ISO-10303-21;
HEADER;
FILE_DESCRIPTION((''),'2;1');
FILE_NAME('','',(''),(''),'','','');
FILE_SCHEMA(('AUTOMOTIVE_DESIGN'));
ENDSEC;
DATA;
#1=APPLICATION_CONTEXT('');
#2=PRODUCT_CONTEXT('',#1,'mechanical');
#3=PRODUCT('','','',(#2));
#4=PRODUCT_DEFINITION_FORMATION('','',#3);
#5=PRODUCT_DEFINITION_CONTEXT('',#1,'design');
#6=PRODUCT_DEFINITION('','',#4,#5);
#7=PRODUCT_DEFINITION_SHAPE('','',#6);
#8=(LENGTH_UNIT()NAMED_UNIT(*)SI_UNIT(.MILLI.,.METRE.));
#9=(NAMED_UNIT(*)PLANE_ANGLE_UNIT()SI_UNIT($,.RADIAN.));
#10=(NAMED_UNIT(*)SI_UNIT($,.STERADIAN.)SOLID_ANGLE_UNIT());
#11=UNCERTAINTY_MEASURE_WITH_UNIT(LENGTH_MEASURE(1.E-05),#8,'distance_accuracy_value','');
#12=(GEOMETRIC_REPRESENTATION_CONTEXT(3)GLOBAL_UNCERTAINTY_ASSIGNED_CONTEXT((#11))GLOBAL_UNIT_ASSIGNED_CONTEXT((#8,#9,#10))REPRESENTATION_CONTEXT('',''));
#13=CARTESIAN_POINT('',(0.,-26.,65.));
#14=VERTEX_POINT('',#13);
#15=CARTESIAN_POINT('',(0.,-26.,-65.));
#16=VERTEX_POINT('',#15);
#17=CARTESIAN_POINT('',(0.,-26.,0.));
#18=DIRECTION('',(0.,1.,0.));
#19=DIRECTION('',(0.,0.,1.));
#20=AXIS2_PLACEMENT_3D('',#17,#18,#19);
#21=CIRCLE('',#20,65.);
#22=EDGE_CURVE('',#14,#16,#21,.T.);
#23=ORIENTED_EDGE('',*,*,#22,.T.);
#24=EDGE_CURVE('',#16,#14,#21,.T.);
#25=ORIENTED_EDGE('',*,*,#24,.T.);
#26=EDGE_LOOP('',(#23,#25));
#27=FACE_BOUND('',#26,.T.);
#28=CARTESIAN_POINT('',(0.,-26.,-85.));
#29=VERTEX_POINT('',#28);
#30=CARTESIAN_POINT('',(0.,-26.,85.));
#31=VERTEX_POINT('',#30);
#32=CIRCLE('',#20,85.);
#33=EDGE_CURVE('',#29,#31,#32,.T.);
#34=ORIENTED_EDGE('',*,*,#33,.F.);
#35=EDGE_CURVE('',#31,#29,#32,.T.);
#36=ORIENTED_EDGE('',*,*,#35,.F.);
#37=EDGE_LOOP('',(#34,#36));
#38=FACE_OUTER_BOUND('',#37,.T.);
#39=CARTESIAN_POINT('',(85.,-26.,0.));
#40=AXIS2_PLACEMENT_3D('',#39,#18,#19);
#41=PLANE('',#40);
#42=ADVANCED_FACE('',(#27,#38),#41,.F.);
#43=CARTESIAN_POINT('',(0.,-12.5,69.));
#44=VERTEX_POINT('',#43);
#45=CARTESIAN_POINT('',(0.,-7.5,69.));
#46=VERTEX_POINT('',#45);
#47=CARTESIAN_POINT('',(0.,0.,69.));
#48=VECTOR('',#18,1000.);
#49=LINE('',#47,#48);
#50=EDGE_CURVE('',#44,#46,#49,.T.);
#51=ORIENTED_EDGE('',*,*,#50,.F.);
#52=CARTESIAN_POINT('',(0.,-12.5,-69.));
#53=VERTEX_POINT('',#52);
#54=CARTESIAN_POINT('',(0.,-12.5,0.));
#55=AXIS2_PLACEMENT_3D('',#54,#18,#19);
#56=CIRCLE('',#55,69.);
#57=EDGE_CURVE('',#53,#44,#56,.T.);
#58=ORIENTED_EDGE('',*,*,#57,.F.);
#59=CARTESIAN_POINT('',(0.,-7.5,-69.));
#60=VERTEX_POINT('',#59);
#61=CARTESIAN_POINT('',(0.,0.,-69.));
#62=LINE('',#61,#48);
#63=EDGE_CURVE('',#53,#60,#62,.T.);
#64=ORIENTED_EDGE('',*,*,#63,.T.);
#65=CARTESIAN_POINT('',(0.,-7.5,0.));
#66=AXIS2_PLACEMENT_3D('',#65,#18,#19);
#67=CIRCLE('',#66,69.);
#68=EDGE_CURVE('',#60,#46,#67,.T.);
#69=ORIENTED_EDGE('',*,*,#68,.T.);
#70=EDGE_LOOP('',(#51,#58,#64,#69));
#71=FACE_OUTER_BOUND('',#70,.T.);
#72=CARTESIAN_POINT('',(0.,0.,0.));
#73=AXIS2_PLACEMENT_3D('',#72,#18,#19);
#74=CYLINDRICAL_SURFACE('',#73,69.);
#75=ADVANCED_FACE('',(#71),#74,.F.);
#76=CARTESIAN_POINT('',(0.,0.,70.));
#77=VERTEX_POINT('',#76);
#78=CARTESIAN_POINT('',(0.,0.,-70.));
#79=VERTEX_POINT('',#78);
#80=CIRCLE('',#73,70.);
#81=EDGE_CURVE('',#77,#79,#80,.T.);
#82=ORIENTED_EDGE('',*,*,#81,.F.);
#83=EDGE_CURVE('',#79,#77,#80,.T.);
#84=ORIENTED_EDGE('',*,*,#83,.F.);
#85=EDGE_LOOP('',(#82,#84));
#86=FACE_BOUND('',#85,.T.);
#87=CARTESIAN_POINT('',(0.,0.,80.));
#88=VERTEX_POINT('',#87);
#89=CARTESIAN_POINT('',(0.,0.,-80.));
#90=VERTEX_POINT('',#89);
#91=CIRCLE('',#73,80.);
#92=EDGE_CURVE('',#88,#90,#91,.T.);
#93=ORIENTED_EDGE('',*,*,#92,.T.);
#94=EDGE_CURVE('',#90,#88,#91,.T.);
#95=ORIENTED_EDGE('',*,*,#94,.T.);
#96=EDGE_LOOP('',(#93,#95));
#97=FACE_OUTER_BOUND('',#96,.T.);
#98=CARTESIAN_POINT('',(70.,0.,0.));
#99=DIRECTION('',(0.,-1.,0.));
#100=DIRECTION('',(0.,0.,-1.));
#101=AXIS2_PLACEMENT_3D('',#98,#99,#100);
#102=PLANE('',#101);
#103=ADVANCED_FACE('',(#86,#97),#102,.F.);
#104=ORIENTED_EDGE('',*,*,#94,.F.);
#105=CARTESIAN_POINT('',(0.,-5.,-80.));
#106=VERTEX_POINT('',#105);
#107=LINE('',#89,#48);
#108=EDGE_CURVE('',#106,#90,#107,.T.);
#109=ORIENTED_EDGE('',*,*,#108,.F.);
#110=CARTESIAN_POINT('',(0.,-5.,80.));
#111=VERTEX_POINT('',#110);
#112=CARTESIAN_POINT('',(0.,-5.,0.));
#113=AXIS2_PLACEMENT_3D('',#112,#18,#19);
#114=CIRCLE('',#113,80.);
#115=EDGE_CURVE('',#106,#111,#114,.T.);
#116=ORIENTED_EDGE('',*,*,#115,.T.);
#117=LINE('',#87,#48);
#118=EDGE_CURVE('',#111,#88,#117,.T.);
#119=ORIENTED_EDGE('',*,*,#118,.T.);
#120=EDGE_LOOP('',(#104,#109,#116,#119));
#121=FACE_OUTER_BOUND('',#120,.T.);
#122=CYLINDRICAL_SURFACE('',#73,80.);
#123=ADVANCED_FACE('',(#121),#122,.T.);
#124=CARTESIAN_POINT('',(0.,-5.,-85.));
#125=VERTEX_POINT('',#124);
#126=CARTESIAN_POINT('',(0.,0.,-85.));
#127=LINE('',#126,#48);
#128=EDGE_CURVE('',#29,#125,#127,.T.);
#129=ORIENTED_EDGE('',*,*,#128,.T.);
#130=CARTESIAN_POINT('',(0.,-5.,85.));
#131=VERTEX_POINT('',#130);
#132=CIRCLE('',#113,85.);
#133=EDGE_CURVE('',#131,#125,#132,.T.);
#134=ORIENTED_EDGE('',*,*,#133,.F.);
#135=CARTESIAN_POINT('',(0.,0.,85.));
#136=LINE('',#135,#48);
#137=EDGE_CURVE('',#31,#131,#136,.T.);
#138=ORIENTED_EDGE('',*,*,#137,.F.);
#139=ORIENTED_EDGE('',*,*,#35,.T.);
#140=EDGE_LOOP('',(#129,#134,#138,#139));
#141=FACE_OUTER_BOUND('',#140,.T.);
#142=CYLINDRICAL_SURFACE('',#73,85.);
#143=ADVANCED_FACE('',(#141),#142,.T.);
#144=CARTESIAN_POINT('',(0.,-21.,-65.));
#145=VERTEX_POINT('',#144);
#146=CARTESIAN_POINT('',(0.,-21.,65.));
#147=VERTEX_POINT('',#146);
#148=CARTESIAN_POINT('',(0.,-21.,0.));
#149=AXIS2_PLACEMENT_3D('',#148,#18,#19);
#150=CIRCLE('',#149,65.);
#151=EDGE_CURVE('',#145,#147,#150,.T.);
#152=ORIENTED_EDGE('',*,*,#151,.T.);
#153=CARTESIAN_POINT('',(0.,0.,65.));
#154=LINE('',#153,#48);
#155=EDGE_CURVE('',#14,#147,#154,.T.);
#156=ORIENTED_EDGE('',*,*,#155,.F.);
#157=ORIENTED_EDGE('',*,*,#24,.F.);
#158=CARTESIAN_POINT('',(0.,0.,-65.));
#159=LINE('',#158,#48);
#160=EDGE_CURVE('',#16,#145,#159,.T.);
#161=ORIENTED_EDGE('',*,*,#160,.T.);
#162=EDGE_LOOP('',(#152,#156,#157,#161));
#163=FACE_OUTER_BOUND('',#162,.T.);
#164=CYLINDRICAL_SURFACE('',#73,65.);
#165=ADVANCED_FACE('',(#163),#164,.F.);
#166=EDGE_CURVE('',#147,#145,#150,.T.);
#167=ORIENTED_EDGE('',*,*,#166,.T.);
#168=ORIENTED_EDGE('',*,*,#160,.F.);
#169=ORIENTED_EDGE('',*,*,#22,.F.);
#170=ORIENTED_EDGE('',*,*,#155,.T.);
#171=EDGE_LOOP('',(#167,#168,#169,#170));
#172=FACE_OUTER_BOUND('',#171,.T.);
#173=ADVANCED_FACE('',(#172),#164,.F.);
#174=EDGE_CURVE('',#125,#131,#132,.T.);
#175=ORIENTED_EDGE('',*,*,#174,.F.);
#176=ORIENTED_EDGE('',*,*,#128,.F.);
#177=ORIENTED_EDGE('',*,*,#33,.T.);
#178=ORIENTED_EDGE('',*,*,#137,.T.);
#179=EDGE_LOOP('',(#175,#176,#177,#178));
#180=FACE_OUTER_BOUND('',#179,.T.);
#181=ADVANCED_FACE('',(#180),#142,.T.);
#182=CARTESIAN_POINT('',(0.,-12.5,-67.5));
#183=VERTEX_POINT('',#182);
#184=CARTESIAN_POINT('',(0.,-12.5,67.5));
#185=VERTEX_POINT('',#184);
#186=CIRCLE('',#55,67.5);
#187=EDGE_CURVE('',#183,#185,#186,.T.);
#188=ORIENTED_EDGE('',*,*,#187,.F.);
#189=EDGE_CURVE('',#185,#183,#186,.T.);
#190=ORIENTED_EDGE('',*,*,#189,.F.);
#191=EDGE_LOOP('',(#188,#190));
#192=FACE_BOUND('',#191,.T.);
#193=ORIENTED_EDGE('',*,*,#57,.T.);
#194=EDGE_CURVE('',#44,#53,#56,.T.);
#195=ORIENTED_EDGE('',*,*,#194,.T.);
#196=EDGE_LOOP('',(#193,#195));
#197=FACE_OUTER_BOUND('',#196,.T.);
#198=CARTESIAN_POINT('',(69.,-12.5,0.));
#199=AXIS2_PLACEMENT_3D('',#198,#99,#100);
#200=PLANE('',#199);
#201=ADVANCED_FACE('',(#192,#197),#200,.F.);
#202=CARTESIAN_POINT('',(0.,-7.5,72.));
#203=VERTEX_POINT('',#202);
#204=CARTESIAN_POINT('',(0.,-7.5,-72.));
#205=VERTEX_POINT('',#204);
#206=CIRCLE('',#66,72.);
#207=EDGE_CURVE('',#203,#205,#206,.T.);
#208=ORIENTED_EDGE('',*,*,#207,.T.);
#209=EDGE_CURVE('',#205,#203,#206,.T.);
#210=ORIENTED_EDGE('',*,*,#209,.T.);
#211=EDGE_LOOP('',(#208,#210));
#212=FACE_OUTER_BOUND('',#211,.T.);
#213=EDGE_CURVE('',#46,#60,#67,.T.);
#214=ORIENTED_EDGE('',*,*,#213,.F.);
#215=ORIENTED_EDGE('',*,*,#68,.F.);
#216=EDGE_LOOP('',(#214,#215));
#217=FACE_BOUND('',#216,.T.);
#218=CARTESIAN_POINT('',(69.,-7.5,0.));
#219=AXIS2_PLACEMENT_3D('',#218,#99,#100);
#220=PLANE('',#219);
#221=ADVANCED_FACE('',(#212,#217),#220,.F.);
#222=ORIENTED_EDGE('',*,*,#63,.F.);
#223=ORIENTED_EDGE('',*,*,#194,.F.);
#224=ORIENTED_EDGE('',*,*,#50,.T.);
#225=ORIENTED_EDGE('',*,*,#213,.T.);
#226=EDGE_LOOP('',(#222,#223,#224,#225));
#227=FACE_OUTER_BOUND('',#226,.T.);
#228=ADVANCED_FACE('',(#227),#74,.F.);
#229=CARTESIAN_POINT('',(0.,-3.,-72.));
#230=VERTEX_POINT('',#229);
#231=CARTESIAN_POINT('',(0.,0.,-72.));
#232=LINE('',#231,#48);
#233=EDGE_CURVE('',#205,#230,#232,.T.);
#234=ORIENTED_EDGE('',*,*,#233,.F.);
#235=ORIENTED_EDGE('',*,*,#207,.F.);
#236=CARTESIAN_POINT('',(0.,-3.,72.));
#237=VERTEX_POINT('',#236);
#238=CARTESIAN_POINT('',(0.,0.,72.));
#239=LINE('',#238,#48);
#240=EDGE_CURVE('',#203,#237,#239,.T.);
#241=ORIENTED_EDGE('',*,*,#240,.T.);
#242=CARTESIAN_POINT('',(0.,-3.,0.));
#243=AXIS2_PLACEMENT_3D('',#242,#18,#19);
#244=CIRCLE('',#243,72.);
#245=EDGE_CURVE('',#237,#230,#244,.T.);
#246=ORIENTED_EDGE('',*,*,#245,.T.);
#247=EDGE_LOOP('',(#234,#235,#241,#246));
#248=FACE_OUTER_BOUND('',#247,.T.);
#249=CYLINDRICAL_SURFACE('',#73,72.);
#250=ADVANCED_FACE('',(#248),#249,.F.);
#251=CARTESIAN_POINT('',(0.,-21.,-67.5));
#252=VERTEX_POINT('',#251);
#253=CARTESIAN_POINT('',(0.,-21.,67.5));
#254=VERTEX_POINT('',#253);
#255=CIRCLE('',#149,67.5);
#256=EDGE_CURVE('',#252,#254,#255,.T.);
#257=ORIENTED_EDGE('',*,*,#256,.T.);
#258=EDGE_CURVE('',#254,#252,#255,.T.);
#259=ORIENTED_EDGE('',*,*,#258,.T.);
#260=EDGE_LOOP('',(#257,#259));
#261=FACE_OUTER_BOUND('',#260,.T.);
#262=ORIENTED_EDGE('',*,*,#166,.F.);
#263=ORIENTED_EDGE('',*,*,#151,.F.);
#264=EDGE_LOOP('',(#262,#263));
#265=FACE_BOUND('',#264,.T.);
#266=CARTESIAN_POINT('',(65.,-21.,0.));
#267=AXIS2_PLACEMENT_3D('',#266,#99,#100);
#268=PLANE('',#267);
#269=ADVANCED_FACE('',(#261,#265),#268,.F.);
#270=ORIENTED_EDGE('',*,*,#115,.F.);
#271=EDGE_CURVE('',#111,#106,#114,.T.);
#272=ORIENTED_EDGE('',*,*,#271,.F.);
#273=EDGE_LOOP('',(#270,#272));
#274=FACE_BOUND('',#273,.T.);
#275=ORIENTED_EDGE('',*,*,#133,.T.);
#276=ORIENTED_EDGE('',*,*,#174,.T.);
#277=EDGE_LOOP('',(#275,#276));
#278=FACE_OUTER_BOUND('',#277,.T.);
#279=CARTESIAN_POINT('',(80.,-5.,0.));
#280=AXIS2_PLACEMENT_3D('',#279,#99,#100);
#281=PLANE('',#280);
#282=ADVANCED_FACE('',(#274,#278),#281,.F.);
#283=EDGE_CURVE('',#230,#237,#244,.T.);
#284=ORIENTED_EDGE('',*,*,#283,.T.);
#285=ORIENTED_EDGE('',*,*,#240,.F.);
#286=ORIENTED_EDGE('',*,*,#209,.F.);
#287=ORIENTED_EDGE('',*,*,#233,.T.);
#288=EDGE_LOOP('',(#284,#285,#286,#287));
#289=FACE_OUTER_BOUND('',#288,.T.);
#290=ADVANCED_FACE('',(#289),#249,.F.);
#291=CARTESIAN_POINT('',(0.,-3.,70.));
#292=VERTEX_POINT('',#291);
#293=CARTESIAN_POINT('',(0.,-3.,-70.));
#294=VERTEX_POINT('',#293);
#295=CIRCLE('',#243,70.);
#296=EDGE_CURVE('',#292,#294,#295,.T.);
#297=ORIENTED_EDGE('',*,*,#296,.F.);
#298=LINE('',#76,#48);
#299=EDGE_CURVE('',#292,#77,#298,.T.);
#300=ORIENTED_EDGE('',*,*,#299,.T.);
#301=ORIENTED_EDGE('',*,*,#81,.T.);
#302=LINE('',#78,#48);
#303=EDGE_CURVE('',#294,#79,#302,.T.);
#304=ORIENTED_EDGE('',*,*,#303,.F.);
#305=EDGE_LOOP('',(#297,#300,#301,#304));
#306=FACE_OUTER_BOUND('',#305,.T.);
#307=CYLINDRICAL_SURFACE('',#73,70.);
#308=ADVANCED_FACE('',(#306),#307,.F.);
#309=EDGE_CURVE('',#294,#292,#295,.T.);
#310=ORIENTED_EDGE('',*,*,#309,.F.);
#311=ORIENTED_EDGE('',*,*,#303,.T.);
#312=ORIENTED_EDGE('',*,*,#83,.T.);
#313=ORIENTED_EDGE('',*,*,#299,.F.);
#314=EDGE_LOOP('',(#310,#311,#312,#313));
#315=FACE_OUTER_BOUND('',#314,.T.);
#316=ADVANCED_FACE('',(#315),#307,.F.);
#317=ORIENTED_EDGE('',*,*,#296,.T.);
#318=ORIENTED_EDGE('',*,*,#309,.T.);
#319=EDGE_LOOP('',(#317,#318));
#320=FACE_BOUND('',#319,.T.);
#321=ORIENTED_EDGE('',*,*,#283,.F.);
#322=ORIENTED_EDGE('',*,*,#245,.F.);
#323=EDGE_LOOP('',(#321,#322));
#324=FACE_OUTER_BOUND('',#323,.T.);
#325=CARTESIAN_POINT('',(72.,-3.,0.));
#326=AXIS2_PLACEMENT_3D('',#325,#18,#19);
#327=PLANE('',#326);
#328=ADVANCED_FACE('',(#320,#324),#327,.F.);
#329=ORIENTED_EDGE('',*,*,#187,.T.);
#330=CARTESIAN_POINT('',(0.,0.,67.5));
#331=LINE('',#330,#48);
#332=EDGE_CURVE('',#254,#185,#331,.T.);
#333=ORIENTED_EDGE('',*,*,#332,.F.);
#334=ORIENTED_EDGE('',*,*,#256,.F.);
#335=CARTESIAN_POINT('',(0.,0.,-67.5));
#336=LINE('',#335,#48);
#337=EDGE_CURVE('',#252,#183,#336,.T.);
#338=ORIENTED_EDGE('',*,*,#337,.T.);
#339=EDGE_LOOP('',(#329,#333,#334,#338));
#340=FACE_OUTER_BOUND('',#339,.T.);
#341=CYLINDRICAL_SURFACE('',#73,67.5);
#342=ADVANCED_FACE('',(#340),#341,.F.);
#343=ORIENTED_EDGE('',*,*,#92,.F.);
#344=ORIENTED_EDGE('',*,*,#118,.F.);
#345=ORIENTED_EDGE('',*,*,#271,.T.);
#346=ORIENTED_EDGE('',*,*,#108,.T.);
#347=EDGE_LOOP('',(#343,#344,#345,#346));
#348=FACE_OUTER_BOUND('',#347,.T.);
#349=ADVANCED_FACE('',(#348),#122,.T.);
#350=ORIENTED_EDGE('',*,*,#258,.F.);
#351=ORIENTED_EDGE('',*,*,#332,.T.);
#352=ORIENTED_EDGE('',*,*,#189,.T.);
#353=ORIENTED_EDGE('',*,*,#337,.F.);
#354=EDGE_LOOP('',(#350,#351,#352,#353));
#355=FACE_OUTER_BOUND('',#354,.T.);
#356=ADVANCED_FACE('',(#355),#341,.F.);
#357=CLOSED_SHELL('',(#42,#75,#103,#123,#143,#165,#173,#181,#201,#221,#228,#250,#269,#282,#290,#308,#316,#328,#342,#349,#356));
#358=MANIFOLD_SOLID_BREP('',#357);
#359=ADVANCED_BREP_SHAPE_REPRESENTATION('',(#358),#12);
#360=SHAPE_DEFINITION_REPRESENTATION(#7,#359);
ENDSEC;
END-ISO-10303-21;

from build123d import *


with BuildPart() as part:
    # Sketch1 → Revolve1 (revolve)
    with BuildSketch(Plane.XY, mode=Mode.PRIVATE) as revolve1_sk:
        Polygon((70, 0), (80, 0), (80, -5), (85, -5), (85, -26), (65, -26), (65, -21), (67.5, -21), (67.5, -12.5), (69, -12.5), (69, -7.5), (72, -7.5), (72, -3), (70, -3), align=None)
    revolve(revolve1_sk.sketch.rotate(Axis((0, 0, 0), (0, -1, 0)), 90), axis=Axis((0, 0, 0), (0, -1, 0)))


solid = part.part
